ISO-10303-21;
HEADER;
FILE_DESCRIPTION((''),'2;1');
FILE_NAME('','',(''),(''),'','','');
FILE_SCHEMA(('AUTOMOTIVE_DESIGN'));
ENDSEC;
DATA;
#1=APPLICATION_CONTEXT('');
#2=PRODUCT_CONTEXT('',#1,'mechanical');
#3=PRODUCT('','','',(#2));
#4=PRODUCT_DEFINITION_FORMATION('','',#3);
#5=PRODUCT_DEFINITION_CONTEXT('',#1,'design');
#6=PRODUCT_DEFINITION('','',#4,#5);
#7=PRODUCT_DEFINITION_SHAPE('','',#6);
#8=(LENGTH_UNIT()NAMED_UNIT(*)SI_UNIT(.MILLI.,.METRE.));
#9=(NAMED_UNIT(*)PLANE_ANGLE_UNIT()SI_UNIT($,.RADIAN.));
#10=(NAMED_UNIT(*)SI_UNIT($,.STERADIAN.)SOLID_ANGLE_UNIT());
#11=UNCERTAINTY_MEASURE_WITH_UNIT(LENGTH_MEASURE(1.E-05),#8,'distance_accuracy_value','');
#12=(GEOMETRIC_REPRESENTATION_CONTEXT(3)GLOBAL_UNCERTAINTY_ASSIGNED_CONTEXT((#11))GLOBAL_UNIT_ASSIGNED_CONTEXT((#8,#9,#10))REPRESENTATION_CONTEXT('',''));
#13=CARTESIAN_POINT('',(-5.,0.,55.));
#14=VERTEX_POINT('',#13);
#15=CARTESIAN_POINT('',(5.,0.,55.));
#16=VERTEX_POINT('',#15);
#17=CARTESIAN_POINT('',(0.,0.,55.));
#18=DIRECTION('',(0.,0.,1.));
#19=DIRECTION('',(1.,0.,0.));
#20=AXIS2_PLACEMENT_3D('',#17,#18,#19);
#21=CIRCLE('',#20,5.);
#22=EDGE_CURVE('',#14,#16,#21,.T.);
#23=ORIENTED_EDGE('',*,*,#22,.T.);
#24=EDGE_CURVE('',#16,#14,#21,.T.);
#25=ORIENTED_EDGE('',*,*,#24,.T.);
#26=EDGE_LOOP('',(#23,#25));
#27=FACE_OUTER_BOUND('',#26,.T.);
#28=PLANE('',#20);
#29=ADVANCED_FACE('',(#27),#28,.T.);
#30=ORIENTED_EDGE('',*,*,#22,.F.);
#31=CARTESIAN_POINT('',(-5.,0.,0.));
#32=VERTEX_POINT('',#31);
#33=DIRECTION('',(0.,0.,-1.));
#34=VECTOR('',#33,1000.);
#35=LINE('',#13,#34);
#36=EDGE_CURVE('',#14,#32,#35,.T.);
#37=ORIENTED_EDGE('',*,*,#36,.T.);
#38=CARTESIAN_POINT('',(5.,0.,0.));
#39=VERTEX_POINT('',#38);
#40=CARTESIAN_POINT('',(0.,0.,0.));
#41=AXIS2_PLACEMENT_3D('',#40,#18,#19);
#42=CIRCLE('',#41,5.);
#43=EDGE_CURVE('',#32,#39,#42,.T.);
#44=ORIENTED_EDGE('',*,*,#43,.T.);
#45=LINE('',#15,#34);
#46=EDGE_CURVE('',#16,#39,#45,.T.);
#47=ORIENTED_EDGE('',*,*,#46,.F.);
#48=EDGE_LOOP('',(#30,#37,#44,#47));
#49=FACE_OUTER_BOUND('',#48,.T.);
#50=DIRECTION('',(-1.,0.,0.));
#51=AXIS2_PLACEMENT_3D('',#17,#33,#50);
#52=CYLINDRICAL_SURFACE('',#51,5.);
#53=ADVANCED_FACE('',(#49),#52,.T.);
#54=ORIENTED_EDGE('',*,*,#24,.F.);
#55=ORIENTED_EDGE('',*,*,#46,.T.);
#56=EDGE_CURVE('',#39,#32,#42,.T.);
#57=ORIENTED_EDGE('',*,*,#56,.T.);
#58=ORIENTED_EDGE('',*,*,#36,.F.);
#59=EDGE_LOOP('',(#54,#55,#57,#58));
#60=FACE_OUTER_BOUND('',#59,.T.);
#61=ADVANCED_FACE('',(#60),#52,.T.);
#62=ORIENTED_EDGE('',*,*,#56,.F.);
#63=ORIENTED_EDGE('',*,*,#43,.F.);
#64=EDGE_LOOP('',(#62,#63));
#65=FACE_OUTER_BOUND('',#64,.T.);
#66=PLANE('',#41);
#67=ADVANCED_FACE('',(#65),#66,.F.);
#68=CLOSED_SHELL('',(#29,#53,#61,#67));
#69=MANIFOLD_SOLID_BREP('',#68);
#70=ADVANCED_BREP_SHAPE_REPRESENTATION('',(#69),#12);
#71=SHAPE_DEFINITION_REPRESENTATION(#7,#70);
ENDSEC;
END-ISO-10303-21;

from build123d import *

# Parameters (mm, degrees)
SKETCH1_R           = 5
BOSS_EXTRUDE1_DEPTH = 55


with BuildPart() as part:
    # Sketch1 → Boss-Extrude1 (new body)
    with BuildSketch(Plane.XY):
        Circle(SKETCH1_R)
    extrude(amount=BOSS_EXTRUDE1_DEPTH)


solid = part.part
